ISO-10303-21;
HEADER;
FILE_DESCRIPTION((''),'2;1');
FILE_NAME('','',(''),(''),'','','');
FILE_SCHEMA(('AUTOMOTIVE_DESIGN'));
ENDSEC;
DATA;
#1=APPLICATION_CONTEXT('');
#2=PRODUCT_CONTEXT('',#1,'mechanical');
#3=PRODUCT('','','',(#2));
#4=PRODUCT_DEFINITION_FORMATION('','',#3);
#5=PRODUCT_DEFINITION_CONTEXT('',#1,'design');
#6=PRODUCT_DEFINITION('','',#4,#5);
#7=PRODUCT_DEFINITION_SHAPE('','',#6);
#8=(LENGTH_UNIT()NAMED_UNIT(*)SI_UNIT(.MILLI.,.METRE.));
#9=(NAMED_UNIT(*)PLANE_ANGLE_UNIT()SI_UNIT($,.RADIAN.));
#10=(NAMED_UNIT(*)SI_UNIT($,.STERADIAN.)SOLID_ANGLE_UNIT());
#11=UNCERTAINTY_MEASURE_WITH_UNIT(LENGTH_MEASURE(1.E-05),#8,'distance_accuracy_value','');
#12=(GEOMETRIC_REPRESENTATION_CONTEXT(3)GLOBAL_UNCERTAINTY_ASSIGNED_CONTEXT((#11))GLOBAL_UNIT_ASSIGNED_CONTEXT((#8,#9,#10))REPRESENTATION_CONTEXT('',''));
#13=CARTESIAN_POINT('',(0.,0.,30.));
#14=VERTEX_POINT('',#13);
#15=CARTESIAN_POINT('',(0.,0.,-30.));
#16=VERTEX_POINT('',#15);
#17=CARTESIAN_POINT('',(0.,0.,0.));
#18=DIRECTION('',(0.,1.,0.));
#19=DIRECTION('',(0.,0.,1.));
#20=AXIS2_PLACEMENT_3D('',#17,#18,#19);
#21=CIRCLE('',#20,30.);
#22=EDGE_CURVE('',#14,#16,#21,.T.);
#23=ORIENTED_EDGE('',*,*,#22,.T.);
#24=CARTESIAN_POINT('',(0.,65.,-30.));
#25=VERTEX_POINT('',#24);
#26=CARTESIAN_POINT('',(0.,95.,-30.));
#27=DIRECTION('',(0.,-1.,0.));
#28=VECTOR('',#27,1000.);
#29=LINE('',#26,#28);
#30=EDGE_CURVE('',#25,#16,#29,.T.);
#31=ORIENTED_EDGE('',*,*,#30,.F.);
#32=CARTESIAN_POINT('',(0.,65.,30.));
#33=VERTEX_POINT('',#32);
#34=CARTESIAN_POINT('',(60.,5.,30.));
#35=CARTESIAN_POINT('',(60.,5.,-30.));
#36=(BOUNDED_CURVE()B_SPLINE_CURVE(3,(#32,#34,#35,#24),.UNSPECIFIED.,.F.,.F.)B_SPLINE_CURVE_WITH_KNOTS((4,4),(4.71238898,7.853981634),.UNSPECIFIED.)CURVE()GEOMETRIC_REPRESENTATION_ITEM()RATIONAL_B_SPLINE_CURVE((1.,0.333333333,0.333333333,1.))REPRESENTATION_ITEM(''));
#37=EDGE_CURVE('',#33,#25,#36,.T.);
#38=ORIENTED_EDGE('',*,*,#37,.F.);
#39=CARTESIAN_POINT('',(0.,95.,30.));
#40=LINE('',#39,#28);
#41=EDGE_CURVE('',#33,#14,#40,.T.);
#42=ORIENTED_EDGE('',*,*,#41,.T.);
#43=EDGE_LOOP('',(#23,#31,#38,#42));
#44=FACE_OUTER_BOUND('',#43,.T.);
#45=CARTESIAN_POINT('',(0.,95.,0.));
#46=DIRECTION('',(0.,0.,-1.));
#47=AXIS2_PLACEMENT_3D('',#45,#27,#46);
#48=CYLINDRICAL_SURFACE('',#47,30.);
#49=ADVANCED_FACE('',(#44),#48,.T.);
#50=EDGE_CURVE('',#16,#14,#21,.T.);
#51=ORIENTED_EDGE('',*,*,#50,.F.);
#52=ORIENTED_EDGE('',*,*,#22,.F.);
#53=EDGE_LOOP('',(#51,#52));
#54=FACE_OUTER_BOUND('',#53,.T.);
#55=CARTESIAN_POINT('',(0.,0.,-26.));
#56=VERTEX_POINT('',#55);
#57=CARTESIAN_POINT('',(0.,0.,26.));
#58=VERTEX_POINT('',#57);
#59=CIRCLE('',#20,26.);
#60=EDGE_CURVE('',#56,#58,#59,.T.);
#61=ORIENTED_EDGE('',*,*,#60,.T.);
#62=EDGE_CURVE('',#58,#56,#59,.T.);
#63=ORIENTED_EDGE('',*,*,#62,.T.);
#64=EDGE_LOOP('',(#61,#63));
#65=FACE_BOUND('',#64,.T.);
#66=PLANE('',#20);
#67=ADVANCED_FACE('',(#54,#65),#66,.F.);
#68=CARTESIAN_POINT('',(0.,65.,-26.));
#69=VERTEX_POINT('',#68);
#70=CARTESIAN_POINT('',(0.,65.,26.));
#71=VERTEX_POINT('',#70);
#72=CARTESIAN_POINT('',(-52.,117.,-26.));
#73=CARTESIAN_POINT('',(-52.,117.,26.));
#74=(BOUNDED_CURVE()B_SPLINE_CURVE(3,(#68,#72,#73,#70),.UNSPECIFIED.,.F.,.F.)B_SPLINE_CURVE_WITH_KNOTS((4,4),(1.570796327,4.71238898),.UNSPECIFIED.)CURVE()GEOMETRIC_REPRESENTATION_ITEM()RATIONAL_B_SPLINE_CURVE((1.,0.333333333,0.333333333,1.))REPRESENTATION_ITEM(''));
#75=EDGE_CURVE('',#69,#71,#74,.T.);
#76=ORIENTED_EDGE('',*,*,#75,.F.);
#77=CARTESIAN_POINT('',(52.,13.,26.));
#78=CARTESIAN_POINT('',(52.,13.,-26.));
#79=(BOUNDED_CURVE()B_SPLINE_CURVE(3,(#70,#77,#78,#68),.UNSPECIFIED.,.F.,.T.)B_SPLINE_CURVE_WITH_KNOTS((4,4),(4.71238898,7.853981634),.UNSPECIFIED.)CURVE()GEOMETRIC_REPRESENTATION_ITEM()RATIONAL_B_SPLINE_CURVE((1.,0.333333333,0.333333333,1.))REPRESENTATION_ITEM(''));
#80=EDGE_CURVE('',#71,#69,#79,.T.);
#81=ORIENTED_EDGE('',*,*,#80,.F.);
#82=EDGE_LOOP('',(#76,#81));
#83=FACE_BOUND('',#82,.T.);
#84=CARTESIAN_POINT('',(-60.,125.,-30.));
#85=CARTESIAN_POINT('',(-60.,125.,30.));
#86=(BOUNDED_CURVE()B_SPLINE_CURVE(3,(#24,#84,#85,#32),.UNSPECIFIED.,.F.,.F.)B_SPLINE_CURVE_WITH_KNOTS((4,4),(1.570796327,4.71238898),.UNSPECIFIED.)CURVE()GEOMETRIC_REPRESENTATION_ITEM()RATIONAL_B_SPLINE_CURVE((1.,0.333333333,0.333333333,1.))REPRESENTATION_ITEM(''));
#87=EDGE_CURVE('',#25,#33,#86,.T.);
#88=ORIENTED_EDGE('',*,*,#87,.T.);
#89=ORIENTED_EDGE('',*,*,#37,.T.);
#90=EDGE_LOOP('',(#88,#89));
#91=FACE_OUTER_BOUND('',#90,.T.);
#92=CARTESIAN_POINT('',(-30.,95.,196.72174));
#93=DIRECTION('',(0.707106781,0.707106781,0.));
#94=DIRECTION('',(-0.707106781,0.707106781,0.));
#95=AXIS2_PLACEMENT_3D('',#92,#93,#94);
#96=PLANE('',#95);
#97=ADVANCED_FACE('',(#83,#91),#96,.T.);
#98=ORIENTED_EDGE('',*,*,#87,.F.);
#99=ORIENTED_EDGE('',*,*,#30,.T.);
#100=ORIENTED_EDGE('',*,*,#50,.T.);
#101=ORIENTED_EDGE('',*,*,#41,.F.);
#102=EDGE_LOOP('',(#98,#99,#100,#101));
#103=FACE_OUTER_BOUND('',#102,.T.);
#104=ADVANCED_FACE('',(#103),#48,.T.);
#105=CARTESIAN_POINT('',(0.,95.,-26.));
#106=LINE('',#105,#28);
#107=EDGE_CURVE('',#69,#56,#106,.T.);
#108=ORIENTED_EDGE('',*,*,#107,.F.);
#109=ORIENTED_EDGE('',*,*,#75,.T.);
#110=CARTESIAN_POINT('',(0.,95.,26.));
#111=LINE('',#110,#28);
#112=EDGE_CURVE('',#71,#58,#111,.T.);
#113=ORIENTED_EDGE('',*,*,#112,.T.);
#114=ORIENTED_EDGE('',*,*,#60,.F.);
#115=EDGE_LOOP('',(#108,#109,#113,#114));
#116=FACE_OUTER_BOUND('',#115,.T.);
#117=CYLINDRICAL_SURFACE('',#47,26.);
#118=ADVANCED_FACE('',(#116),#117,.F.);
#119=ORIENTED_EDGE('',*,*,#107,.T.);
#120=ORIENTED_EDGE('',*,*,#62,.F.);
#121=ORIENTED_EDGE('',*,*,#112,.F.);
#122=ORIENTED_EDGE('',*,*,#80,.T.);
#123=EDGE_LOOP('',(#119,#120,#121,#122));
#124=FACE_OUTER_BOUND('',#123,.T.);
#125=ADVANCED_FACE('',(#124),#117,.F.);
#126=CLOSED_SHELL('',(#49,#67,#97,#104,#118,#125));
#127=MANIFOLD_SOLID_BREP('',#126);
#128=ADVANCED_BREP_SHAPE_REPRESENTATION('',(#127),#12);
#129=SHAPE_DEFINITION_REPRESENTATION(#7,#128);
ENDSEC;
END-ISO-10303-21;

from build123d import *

# Parameters (mm, degrees)
SKETCH1_R               = 30
SKETCH1_R_2             = 26
BOSS_EXTRUDE1_DEPTH     = 95
CUT_EXTRUDE1_DEPTH      = 105.043260233
CUT_EXTRUDE1_DEPTH_BACK = 105.043260233


with BuildPart() as part:
    # Sketch1 → Boss-Extrude1 (new body)
    with BuildSketch(Plane(origin=(0, 0, 0), x_dir=(1, 0, 0), z_dir=(0, 1, 0))):
        with Locations(Location((0, 0, 0), (0, 0, 270))):
            Circle(SKETCH1_R)
        with Locations(Location((0, 0, 0), (0, 0, 270))):
            Circle(SKETCH1_R_2, mode=Mode.SUBTRACT)
    extrude(amount=BOSS_EXTRUDE1_DEPTH)

    # Sketch2 → Cut-Extrude1 (cut, two sides: drawn at the far end of the back side and taken through both)
    with BuildSketch(Plane.XY.offset(-CUT_EXTRUDE1_DEPTH_BACK)):
        Polygon((-195.973553633, 260.973553633), (-30, 95), (45.712319076, 19.287680924), (211.685872708, -146.685872708), (543.632979974, 185.261234557), (135.973553633, 592.920660898), align=None)
    extrude(amount=CUT_EXTRUDE1_DEPTH + CUT_EXTRUDE1_DEPTH_BACK, mode=Mode.SUBTRACT)


solid = part.part
